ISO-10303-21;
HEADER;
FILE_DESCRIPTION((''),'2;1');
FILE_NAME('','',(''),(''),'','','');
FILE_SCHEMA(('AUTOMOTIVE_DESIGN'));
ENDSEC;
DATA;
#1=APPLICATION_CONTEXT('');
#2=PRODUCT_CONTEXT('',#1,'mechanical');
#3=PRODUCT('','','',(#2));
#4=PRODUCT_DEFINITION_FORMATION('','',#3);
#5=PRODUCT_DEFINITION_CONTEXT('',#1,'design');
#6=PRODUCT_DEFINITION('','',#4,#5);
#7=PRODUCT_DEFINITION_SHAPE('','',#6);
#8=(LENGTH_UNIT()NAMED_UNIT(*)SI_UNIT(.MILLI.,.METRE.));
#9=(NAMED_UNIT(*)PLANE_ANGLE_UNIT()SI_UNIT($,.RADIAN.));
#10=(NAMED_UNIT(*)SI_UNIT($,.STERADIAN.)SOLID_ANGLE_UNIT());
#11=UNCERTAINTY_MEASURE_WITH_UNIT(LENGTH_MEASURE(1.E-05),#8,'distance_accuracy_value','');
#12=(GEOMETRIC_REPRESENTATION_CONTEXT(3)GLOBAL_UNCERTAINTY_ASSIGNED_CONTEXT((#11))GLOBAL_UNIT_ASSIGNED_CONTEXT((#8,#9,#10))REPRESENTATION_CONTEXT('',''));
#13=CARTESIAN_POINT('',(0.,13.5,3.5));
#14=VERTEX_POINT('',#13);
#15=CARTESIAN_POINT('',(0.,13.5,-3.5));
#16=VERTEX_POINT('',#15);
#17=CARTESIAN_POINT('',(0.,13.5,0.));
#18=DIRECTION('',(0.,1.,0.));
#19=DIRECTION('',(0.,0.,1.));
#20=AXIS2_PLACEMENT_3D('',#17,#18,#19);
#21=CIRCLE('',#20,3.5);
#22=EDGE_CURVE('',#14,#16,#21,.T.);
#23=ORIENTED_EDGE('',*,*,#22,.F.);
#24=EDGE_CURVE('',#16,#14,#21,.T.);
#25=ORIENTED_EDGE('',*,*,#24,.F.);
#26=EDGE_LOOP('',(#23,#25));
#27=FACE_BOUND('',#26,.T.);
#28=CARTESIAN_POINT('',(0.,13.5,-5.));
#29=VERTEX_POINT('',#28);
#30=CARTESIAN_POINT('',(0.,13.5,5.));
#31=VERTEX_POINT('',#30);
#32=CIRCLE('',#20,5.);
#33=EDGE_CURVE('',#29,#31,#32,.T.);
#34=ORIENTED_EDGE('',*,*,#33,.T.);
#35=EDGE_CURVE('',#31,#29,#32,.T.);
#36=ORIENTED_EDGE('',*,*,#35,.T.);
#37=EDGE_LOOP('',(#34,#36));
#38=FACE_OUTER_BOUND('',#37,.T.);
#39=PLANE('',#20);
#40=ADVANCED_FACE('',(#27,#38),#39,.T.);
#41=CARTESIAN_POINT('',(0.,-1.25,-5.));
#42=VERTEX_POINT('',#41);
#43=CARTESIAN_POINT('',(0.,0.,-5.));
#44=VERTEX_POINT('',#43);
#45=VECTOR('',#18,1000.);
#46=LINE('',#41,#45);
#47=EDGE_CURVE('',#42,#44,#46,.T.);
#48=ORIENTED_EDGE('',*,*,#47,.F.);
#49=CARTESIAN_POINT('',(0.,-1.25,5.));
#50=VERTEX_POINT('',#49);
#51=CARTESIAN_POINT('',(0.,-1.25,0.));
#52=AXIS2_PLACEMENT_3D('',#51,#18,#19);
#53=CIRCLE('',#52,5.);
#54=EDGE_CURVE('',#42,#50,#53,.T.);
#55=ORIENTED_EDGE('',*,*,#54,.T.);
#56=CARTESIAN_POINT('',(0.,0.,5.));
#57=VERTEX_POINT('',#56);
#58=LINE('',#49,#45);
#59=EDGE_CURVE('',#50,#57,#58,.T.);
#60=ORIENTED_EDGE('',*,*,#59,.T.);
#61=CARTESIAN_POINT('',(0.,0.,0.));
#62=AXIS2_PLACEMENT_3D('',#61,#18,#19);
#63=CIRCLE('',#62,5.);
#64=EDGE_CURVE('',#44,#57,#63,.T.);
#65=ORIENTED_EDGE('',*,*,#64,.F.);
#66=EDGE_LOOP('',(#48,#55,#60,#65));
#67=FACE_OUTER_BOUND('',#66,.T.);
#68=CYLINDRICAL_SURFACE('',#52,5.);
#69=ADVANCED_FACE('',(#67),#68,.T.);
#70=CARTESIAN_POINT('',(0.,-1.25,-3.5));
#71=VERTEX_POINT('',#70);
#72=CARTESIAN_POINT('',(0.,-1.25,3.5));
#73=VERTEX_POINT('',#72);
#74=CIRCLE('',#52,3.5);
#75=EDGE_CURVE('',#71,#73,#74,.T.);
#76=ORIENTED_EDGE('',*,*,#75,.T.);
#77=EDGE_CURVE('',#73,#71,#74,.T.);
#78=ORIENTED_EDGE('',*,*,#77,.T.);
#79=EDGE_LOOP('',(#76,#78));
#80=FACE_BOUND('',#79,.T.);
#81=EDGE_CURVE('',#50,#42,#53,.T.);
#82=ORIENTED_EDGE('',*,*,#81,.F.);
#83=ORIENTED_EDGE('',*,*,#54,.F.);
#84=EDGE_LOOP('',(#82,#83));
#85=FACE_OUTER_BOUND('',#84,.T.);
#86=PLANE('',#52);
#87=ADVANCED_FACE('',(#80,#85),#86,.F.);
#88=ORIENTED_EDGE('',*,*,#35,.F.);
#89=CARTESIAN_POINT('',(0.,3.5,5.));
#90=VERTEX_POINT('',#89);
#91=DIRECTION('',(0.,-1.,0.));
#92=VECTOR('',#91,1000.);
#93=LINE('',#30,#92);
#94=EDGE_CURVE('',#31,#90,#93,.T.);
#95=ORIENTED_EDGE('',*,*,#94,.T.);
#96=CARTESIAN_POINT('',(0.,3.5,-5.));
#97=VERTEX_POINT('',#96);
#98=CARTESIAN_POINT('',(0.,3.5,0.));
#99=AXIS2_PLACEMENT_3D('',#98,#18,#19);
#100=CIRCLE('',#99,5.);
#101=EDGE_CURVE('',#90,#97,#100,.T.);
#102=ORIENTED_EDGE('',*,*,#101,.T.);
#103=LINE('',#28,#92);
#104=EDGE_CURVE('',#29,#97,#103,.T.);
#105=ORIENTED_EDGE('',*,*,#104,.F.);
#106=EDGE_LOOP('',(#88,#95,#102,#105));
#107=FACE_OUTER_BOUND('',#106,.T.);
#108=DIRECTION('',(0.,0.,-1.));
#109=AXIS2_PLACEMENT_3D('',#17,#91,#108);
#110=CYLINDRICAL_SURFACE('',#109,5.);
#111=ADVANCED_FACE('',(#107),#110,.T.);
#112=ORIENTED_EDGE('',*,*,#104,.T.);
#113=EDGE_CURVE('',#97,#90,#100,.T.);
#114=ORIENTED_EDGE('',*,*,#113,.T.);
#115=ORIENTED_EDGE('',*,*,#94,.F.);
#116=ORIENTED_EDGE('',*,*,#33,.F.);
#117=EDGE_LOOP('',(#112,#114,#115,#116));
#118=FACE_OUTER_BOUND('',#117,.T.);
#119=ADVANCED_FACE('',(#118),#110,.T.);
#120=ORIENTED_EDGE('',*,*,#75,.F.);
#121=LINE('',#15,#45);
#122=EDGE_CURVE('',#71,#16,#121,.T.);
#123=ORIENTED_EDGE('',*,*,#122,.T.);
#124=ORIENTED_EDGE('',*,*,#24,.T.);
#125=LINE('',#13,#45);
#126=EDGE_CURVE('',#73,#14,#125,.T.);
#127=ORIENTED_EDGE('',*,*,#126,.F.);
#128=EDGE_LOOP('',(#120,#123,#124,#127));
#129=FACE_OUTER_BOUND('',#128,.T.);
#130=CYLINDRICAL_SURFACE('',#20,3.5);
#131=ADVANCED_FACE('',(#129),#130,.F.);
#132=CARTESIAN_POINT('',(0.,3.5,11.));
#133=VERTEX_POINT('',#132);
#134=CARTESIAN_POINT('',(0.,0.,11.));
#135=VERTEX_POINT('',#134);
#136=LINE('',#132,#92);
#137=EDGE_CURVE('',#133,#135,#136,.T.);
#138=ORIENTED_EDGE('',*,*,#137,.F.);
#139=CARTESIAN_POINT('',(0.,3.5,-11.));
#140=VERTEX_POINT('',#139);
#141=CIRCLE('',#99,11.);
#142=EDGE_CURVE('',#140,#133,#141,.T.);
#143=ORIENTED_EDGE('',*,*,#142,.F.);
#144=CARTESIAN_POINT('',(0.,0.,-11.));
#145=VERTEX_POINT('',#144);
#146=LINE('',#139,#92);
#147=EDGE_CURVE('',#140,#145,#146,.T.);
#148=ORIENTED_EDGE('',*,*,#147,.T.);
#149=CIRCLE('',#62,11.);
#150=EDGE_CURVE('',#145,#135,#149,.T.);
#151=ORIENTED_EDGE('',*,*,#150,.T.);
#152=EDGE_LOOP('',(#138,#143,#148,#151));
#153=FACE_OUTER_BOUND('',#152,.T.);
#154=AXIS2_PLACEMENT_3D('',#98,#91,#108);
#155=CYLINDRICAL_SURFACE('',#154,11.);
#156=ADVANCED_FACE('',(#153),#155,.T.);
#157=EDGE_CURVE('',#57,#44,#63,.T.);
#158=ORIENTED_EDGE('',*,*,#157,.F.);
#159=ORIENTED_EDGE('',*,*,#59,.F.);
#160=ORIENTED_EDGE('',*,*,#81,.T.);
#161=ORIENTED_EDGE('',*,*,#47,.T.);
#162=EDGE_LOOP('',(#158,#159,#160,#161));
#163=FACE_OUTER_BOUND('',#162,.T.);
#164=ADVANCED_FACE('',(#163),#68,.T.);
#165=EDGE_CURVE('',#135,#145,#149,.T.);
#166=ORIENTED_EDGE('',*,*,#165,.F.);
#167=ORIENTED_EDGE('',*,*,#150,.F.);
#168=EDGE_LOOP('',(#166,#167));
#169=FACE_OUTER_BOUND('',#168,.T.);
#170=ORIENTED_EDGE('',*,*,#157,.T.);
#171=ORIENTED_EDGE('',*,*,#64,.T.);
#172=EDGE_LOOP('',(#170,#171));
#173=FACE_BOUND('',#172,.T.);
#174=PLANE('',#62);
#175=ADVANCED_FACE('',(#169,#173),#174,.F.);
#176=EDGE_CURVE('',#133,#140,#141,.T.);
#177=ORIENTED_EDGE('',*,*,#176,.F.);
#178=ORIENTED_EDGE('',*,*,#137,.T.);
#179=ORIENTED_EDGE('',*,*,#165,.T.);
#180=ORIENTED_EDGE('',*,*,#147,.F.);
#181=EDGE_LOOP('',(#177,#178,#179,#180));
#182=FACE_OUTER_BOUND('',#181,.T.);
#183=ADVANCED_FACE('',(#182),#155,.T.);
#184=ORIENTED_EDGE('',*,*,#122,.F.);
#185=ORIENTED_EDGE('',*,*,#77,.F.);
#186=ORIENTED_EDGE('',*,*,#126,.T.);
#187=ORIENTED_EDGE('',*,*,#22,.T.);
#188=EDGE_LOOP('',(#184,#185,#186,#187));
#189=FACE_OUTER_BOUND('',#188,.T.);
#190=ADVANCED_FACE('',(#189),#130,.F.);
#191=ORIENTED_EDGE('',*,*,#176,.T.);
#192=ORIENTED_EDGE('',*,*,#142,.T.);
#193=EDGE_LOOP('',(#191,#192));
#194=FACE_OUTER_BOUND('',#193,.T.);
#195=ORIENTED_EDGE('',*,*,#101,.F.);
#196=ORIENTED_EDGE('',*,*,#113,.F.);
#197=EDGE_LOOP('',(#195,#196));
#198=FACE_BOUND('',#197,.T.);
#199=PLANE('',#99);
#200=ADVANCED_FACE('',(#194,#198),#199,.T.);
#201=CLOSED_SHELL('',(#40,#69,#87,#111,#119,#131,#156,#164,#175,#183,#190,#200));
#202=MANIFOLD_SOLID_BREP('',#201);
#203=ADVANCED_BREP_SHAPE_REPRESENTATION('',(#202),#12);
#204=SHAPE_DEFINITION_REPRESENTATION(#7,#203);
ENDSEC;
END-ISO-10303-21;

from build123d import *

# Parameters (mm, degrees)
SKETCH1_R             = 11
SKETCH1_R_2           = 5
BOSS_EXTRUDE1_DEPTH   = 3.5
SKETCH1_2_R           = 5
BOSS_EXTRUDE2_DEPTH   = 1.25
SKETCH1_3_R           = 5
BOSS_EXTRUDE3_DEPTH   = 13.5
M8X1_0_TAPPED_HOLE1_D = 7


with BuildPart() as part:
    # Sketch1 → Boss-Extrude1 (new body)
    with BuildSketch(Plane(origin=(0, 0, 0), x_dir=(1, 0, 0), z_dir=(0, 1, 0))):
        with Locations(Location((0, 0, 0), (0, 0, 270))):
            Circle(SKETCH1_R)
        with Locations(Location((0, 0, 0), (0, 0, 270))):
            Circle(SKETCH1_R_2, mode=Mode.SUBTRACT)
    extrude(amount=BOSS_EXTRUDE1_DEPTH)



with BuildPart() as body_2:
    # Sketch1<2> → Boss-Extrude2 (new body)
    with BuildSketch(Plane(origin=(0, 0, 0), x_dir=(1, 0, 0), z_dir=(0, 1, 0))):
        with Locations(Location((0, 0, 0), (0, 0, 270))):
            Circle(SKETCH1_2_R)
    extrude(amount=-BOSS_EXTRUDE2_DEPTH)


with BuildPart() as part_1:
    add(part.part)

    add(body_2.part)  # Boss-Extrude3 merges body 2
    # Sketch1<3> → Boss-Extrude3 (add)
    with BuildSketch(Plane(origin=(0, 0, 0), x_dir=(1, 0, 0), z_dir=(0, 1, 0))):
        with Locations(Location((0, 0, 0), (0, 0, 270))):
            Circle(SKETCH1_3_R)
    extrude(amount=BOSS_EXTRUDE3_DEPTH)

    # M8x1.0 Tapped Hole1 (through all)
    with Locations(Plane.ZX.offset(13.5)):
        with Locations((0, 0)):
            Hole(M8X1_0_TAPPED_HOLE1_D / 2)


solid = part_1.part
